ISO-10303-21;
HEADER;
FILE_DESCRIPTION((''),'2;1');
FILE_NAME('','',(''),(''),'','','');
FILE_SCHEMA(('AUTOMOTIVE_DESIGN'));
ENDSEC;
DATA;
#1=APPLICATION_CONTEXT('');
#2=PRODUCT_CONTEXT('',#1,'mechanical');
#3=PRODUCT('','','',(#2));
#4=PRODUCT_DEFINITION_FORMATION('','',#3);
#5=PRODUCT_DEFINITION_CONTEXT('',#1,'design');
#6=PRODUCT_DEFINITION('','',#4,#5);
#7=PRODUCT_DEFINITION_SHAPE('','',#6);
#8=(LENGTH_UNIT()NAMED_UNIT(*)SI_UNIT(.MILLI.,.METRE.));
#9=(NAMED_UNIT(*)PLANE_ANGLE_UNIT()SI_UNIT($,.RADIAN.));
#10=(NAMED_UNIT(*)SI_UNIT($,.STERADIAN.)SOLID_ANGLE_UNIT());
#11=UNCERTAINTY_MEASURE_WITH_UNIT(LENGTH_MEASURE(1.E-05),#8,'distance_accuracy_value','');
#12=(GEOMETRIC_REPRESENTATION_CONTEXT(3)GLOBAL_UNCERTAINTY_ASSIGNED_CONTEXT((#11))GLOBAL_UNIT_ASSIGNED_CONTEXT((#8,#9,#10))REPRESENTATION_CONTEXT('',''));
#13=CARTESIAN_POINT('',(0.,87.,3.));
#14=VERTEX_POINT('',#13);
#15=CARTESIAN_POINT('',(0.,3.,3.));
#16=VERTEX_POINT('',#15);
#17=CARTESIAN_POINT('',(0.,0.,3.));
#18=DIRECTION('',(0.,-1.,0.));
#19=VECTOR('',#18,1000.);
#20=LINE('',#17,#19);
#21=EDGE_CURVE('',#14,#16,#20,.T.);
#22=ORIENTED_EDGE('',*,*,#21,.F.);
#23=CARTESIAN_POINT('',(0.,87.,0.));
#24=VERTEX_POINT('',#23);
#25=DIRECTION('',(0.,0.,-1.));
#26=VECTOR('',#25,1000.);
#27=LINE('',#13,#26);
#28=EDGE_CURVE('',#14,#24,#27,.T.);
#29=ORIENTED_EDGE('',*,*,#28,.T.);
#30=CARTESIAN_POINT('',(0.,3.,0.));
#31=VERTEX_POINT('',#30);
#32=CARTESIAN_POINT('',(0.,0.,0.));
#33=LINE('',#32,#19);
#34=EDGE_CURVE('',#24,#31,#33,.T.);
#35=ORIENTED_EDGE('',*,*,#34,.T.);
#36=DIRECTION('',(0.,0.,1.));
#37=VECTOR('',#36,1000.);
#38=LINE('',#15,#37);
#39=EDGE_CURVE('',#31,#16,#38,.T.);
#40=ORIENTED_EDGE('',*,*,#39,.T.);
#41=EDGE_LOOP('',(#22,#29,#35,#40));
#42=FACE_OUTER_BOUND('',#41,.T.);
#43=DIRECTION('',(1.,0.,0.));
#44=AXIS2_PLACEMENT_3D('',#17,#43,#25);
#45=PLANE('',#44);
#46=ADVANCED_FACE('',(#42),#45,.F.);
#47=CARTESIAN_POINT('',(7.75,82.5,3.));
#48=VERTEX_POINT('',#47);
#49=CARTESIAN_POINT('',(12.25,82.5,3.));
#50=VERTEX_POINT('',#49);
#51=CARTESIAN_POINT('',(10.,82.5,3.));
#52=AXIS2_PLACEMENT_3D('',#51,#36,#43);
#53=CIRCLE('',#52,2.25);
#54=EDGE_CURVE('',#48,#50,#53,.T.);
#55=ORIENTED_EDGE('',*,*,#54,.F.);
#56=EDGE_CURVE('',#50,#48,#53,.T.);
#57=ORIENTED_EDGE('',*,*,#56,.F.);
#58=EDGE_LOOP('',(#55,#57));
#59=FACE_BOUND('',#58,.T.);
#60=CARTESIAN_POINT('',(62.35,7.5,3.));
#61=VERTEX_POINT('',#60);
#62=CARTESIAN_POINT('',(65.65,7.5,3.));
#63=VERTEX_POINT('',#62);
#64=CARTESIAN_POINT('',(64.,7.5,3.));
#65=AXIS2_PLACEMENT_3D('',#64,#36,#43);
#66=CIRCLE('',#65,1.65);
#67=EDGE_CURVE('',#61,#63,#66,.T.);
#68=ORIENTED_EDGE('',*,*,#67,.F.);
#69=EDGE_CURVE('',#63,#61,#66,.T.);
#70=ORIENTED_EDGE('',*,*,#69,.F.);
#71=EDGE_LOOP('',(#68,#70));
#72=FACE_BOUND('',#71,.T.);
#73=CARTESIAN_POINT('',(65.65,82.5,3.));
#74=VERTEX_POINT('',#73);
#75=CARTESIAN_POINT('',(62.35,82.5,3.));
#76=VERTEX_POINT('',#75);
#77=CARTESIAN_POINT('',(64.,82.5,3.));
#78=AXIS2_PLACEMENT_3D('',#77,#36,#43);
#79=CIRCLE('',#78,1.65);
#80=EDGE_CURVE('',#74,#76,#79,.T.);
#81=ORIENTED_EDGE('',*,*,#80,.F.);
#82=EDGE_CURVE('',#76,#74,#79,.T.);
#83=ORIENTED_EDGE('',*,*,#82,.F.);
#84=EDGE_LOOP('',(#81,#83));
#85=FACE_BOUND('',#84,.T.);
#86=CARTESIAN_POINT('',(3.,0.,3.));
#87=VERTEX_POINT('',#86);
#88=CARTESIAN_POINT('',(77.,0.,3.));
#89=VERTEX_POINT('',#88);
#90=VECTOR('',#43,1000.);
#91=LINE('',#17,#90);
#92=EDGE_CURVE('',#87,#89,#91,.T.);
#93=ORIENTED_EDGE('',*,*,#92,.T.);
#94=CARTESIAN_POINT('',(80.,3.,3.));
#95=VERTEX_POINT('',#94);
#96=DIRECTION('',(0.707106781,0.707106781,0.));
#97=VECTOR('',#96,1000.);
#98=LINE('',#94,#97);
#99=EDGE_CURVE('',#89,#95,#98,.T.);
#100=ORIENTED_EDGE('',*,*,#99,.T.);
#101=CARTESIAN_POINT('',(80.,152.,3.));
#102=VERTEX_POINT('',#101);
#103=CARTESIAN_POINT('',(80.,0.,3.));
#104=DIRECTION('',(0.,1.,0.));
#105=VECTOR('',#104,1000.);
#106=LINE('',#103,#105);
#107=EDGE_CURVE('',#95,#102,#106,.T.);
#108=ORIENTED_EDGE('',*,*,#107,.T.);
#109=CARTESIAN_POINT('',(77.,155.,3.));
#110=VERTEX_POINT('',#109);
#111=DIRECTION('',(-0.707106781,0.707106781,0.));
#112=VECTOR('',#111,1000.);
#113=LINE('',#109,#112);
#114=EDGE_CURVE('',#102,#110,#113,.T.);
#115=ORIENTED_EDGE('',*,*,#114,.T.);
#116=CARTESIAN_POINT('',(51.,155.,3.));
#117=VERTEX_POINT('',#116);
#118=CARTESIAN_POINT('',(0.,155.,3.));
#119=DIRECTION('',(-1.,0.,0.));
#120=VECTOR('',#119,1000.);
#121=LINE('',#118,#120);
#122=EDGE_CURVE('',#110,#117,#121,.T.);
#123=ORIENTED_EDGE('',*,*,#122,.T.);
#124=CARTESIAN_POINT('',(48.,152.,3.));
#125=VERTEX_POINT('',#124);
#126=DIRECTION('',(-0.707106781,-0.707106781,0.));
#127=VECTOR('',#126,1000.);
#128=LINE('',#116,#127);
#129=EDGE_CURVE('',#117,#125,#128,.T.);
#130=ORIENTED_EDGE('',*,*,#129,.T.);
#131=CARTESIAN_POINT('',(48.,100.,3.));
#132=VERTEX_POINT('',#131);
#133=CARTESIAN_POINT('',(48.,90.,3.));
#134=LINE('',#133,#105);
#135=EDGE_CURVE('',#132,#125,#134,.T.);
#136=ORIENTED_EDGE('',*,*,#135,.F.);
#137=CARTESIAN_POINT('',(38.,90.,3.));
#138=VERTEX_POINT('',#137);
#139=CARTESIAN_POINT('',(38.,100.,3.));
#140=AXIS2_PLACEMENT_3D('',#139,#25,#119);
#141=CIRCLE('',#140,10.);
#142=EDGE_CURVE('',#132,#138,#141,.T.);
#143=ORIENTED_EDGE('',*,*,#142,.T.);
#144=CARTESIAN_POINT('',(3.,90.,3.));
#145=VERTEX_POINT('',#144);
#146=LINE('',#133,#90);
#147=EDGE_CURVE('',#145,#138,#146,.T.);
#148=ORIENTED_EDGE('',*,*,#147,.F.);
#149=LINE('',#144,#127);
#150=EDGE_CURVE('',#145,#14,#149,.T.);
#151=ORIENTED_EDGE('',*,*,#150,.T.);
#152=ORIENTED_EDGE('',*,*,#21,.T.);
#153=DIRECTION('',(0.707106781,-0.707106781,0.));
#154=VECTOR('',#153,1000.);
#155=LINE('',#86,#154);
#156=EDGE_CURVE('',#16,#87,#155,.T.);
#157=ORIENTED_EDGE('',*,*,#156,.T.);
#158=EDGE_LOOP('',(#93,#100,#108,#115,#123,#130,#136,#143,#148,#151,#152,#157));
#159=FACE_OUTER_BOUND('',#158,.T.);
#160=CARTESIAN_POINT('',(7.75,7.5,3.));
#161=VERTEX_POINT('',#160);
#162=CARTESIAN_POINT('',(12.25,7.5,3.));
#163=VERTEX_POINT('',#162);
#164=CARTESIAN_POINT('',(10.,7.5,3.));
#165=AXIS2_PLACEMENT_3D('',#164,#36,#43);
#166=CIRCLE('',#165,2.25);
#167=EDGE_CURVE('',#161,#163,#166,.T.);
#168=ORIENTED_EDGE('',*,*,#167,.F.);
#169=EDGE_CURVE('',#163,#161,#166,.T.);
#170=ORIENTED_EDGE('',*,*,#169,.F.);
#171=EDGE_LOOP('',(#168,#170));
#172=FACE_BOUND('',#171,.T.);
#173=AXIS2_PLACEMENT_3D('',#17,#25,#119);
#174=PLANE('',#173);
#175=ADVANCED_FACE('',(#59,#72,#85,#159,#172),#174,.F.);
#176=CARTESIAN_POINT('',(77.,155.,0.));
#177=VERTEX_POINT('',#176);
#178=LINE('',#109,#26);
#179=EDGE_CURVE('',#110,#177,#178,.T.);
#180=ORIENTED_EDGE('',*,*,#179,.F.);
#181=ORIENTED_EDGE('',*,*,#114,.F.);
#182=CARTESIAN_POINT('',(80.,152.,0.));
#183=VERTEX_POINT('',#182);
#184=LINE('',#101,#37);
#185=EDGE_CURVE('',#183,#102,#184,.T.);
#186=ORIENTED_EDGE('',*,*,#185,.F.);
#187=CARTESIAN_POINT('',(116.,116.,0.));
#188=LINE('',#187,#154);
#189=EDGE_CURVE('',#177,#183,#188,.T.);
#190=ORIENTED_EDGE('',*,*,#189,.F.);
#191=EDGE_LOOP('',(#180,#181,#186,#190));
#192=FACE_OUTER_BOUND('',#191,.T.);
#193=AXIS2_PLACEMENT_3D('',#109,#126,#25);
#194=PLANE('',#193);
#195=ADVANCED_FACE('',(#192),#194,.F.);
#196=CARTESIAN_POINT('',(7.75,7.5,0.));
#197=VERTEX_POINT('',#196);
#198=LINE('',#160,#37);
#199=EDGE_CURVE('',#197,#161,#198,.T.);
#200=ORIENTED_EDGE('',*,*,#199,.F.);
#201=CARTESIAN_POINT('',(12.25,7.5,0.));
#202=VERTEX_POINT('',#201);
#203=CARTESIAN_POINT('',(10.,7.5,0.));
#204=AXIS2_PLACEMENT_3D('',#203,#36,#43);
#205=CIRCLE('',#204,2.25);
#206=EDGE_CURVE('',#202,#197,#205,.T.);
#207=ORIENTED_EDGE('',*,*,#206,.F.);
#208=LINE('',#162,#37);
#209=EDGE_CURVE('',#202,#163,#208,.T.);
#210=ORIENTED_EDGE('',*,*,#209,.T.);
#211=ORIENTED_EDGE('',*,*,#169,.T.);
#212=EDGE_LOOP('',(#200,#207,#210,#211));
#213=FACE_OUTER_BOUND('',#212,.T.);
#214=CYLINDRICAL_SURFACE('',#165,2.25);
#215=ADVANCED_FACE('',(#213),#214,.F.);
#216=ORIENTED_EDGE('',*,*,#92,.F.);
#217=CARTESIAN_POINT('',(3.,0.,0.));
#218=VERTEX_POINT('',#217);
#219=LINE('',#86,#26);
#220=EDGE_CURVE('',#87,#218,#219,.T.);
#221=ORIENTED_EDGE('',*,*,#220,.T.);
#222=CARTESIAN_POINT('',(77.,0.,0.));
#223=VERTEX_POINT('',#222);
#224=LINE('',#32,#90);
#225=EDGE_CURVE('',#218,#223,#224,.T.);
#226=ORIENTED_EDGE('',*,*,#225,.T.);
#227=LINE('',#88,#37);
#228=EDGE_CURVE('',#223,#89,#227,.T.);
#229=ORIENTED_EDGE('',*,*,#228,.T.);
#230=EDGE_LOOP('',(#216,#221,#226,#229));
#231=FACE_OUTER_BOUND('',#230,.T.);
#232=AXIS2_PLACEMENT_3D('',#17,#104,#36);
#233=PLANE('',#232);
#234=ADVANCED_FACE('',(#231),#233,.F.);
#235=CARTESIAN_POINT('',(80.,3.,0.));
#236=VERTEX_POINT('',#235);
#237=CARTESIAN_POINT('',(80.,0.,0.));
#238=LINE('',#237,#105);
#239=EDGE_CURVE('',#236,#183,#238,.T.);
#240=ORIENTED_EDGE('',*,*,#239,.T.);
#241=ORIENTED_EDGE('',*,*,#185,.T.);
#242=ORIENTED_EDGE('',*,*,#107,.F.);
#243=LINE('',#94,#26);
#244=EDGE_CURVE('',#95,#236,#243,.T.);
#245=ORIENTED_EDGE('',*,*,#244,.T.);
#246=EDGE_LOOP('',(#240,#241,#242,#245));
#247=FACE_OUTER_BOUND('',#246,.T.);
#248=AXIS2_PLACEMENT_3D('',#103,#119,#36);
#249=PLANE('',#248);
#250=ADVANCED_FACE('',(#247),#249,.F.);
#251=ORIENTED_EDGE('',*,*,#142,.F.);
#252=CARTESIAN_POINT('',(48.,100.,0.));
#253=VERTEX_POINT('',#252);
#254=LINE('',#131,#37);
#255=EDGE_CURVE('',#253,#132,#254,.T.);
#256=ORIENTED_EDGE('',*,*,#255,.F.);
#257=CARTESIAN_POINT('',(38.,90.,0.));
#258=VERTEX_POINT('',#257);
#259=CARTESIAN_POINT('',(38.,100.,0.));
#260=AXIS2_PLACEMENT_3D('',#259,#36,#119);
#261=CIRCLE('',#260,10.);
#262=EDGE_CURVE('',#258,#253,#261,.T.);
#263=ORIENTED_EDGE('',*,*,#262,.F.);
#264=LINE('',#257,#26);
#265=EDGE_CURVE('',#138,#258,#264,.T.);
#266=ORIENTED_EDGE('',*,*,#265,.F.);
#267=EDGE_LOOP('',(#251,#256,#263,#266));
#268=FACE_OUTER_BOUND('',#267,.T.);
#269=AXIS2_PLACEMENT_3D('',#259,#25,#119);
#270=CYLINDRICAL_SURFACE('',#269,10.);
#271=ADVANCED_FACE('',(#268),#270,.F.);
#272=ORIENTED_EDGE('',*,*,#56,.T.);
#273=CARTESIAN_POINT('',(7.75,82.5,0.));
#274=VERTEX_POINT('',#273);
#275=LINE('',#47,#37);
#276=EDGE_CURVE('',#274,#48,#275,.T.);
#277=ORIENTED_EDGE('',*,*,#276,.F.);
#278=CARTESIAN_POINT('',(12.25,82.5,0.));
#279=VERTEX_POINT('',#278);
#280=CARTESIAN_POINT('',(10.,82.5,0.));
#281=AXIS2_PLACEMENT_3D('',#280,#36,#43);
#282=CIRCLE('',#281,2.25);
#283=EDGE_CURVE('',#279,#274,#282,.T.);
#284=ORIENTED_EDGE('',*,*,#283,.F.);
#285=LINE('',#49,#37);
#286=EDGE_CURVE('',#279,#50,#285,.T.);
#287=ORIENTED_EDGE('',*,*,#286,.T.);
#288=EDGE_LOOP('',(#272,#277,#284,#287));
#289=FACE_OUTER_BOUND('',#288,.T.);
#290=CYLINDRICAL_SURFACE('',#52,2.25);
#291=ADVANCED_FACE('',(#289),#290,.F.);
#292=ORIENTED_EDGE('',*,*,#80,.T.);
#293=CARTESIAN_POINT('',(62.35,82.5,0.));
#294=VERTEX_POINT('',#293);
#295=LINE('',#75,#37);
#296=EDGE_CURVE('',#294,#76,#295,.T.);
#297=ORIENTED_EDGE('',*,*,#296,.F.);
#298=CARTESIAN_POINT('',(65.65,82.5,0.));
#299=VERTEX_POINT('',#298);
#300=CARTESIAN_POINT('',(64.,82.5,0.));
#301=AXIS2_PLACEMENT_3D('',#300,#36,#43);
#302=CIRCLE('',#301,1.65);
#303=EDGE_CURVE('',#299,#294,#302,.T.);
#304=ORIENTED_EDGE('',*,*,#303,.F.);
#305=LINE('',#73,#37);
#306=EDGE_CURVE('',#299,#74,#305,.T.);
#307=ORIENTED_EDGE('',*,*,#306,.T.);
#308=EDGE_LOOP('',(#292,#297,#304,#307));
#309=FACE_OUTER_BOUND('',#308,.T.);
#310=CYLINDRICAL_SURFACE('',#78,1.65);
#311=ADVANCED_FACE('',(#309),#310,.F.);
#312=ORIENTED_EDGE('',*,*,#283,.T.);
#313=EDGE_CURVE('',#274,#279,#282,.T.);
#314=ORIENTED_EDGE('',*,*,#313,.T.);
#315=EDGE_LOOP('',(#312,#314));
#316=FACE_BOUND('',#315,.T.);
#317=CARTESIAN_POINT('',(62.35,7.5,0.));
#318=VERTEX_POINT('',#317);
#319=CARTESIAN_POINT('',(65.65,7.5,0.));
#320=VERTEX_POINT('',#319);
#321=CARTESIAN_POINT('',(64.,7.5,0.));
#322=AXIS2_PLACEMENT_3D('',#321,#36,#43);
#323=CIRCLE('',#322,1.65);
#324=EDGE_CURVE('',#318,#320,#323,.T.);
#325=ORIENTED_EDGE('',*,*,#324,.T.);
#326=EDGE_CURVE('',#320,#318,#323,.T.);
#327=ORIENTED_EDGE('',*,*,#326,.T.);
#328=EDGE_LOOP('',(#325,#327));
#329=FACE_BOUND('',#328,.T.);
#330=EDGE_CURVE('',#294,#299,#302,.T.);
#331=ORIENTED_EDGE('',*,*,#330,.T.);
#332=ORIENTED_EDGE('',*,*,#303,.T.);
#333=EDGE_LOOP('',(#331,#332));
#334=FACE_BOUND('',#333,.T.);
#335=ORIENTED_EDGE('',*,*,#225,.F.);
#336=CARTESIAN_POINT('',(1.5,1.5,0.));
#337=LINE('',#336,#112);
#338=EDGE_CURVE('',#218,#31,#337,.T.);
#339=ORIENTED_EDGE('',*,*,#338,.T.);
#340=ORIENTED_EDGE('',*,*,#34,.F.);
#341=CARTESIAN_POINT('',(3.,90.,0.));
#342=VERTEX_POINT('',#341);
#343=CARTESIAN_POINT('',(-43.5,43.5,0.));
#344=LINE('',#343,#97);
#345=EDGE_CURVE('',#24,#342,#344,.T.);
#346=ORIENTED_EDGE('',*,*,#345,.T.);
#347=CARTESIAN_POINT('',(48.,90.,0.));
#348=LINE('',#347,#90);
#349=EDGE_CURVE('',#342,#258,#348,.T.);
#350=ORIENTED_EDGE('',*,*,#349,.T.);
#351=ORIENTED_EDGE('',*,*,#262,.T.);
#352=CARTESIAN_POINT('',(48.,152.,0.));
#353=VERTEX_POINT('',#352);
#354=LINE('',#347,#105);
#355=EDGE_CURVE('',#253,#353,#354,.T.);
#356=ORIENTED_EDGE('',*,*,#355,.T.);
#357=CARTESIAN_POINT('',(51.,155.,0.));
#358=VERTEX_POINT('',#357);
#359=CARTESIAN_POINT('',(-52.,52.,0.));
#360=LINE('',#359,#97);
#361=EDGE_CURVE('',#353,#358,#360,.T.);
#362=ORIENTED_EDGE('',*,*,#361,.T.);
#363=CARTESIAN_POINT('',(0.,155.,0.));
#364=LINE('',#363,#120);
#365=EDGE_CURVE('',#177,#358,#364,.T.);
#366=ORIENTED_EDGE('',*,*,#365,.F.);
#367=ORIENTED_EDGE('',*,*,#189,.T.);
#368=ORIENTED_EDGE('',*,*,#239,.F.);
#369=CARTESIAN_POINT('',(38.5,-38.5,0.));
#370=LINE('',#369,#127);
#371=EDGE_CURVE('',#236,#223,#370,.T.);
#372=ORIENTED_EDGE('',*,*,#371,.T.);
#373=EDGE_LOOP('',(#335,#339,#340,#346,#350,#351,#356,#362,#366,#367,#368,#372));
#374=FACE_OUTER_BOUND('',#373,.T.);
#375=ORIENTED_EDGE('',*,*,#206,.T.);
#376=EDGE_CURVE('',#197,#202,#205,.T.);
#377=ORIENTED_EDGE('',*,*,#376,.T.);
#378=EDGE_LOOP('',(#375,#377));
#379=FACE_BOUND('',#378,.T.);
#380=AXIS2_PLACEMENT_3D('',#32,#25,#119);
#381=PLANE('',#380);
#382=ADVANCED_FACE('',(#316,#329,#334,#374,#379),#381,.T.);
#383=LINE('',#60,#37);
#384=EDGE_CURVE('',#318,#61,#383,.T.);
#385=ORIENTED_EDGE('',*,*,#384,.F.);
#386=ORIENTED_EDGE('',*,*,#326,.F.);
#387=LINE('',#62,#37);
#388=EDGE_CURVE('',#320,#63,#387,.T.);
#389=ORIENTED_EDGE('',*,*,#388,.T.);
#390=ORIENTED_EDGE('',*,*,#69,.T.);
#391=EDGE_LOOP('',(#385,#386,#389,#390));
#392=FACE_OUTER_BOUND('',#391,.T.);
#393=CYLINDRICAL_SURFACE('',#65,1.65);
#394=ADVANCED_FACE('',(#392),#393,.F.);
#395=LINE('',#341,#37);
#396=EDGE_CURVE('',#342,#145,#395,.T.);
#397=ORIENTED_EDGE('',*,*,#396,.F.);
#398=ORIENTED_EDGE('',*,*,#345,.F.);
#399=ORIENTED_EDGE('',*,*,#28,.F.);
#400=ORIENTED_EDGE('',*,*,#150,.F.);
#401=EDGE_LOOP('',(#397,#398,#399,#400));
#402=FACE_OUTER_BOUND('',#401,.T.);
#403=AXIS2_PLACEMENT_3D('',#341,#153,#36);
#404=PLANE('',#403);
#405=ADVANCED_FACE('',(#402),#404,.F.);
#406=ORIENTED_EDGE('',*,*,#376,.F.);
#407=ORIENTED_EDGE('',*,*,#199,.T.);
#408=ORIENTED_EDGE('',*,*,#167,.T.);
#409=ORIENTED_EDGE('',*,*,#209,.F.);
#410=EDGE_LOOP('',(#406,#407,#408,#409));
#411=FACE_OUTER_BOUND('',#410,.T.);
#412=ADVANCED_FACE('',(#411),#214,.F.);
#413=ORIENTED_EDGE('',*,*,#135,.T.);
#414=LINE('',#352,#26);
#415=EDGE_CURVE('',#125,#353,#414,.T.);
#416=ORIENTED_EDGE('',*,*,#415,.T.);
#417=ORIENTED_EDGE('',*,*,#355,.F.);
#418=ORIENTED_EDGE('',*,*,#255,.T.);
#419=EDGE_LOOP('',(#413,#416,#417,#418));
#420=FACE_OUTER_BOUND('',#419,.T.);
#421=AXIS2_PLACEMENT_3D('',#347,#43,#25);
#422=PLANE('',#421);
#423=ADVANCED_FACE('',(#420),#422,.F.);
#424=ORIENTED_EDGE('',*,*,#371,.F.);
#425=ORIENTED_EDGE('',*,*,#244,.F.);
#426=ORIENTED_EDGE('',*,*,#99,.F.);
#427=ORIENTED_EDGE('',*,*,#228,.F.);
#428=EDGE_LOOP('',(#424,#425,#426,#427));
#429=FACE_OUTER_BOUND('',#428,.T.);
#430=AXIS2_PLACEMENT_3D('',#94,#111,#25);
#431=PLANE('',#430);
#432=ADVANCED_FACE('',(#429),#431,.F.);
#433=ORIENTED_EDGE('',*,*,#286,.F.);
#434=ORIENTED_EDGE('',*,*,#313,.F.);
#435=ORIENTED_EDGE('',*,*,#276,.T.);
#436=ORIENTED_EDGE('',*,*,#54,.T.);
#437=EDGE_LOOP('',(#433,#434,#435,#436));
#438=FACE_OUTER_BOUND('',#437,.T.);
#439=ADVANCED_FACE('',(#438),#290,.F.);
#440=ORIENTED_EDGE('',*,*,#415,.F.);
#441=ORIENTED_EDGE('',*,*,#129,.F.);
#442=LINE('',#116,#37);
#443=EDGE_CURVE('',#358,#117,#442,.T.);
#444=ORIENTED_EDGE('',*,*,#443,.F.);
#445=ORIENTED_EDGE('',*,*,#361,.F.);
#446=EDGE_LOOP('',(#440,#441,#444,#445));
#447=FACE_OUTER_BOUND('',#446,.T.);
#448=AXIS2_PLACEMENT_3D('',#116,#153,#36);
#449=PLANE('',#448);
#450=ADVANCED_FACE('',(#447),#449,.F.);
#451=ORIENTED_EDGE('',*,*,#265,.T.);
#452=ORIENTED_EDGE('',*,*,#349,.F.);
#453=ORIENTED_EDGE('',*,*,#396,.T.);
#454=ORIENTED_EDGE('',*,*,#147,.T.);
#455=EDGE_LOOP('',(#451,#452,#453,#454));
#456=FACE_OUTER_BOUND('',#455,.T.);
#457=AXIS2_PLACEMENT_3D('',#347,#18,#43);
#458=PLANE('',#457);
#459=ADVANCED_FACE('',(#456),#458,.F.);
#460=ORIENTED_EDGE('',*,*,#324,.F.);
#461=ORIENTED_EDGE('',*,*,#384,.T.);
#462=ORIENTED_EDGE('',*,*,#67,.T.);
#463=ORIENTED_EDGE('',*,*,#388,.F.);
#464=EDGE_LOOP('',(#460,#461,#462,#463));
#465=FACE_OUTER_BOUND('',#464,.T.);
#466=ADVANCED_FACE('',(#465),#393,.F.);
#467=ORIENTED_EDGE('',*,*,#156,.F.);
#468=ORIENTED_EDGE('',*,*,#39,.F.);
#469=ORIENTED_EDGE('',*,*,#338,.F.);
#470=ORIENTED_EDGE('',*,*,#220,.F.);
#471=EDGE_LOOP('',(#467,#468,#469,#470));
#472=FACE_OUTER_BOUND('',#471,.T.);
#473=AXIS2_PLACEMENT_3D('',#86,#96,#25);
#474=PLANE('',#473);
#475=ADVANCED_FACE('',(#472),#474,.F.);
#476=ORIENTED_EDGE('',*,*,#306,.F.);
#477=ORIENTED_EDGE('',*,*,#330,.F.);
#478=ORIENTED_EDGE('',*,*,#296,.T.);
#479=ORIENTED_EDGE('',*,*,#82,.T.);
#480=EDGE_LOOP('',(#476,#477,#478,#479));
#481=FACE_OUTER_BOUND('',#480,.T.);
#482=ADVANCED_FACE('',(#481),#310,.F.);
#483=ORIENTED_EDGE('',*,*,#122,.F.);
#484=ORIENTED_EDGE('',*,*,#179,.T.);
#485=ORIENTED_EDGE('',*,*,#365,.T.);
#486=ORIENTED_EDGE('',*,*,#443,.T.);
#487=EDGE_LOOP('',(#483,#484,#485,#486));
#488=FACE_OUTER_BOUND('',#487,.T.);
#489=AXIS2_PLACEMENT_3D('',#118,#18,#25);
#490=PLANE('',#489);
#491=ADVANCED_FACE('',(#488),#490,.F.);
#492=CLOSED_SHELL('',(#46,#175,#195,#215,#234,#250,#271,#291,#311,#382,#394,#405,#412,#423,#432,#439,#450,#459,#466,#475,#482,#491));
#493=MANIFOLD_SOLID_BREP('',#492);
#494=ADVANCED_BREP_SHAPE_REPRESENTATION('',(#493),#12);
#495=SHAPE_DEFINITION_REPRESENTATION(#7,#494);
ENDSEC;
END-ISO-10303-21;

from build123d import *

# Parameters (mm, degrees)
SKETCH1_W            = 80
SKETCH1_H            = 155
BOSS_EXTRUDE1_DEPTH  = 3
M4_TAPPED_HOLE1_D    = 3.3
M4_CLEARANCE_HOLE1_D = 4.5
SKETCH8_W            = 48
SKETCH8_H            = 65
CUT_EXTRUDE1_DEPTH   = 175.453432182
CHAMFER1_SIZE        = 3
FILLET1_R            = 10


with BuildPart() as part:
    # Sketch1 → Boss-Extrude1 (new body)
    with BuildSketch(Plane.XY):
        with Locations((40, 77.5)):
            Rectangle(SKETCH1_W, SKETCH1_H)
    extrude(amount=BOSS_EXTRUDE1_DEPTH)

    # M4 Tapped Hole1 (through all)
    with Locations(Plane.XY.offset(3)):
        with Locations((64, 82.5), (64, 7.5)):
            Hole(M4_TAPPED_HOLE1_D / 2)

    # M4 Clearance Hole1 (through all)
    with Locations(Plane.XY.offset(3)):
        with Locations((10, 82.5), (10, 7.5)):
            Hole(M4_CLEARANCE_HOLE1_D / 2)

    # Sketch8 → Cut-Extrude1 (cut, through all)
    with BuildSketch(Plane.XY.offset(3)):
        with Locations((24, 122.5)):
            Rectangle(SKETCH8_W, SKETCH8_H)
    extrude(amount=-CUT_EXTRUDE1_DEPTH, mode=Mode.SUBTRACT)

    # Chamfer1
    chamfer1_edges = [part.edges().sort_by_distance(p)[0] for p in [
        (48, 155, 1.5),
        (0, 90, 1.5),
        (80, 155, 1.5),
        (80, 0, 1.5),
        (0, 0, 1.5),
    ]]
    chamfer(chamfer1_edges, length=CHAMFER1_SIZE)

    # Fillet1
    fillet1_edges = [part.edges().sort_by_distance(p)[0] for p in [
        (48, 90, 1.5),
    ]]
    fillet(fillet1_edges, radius=FILLET1_R)


solid = part.part
